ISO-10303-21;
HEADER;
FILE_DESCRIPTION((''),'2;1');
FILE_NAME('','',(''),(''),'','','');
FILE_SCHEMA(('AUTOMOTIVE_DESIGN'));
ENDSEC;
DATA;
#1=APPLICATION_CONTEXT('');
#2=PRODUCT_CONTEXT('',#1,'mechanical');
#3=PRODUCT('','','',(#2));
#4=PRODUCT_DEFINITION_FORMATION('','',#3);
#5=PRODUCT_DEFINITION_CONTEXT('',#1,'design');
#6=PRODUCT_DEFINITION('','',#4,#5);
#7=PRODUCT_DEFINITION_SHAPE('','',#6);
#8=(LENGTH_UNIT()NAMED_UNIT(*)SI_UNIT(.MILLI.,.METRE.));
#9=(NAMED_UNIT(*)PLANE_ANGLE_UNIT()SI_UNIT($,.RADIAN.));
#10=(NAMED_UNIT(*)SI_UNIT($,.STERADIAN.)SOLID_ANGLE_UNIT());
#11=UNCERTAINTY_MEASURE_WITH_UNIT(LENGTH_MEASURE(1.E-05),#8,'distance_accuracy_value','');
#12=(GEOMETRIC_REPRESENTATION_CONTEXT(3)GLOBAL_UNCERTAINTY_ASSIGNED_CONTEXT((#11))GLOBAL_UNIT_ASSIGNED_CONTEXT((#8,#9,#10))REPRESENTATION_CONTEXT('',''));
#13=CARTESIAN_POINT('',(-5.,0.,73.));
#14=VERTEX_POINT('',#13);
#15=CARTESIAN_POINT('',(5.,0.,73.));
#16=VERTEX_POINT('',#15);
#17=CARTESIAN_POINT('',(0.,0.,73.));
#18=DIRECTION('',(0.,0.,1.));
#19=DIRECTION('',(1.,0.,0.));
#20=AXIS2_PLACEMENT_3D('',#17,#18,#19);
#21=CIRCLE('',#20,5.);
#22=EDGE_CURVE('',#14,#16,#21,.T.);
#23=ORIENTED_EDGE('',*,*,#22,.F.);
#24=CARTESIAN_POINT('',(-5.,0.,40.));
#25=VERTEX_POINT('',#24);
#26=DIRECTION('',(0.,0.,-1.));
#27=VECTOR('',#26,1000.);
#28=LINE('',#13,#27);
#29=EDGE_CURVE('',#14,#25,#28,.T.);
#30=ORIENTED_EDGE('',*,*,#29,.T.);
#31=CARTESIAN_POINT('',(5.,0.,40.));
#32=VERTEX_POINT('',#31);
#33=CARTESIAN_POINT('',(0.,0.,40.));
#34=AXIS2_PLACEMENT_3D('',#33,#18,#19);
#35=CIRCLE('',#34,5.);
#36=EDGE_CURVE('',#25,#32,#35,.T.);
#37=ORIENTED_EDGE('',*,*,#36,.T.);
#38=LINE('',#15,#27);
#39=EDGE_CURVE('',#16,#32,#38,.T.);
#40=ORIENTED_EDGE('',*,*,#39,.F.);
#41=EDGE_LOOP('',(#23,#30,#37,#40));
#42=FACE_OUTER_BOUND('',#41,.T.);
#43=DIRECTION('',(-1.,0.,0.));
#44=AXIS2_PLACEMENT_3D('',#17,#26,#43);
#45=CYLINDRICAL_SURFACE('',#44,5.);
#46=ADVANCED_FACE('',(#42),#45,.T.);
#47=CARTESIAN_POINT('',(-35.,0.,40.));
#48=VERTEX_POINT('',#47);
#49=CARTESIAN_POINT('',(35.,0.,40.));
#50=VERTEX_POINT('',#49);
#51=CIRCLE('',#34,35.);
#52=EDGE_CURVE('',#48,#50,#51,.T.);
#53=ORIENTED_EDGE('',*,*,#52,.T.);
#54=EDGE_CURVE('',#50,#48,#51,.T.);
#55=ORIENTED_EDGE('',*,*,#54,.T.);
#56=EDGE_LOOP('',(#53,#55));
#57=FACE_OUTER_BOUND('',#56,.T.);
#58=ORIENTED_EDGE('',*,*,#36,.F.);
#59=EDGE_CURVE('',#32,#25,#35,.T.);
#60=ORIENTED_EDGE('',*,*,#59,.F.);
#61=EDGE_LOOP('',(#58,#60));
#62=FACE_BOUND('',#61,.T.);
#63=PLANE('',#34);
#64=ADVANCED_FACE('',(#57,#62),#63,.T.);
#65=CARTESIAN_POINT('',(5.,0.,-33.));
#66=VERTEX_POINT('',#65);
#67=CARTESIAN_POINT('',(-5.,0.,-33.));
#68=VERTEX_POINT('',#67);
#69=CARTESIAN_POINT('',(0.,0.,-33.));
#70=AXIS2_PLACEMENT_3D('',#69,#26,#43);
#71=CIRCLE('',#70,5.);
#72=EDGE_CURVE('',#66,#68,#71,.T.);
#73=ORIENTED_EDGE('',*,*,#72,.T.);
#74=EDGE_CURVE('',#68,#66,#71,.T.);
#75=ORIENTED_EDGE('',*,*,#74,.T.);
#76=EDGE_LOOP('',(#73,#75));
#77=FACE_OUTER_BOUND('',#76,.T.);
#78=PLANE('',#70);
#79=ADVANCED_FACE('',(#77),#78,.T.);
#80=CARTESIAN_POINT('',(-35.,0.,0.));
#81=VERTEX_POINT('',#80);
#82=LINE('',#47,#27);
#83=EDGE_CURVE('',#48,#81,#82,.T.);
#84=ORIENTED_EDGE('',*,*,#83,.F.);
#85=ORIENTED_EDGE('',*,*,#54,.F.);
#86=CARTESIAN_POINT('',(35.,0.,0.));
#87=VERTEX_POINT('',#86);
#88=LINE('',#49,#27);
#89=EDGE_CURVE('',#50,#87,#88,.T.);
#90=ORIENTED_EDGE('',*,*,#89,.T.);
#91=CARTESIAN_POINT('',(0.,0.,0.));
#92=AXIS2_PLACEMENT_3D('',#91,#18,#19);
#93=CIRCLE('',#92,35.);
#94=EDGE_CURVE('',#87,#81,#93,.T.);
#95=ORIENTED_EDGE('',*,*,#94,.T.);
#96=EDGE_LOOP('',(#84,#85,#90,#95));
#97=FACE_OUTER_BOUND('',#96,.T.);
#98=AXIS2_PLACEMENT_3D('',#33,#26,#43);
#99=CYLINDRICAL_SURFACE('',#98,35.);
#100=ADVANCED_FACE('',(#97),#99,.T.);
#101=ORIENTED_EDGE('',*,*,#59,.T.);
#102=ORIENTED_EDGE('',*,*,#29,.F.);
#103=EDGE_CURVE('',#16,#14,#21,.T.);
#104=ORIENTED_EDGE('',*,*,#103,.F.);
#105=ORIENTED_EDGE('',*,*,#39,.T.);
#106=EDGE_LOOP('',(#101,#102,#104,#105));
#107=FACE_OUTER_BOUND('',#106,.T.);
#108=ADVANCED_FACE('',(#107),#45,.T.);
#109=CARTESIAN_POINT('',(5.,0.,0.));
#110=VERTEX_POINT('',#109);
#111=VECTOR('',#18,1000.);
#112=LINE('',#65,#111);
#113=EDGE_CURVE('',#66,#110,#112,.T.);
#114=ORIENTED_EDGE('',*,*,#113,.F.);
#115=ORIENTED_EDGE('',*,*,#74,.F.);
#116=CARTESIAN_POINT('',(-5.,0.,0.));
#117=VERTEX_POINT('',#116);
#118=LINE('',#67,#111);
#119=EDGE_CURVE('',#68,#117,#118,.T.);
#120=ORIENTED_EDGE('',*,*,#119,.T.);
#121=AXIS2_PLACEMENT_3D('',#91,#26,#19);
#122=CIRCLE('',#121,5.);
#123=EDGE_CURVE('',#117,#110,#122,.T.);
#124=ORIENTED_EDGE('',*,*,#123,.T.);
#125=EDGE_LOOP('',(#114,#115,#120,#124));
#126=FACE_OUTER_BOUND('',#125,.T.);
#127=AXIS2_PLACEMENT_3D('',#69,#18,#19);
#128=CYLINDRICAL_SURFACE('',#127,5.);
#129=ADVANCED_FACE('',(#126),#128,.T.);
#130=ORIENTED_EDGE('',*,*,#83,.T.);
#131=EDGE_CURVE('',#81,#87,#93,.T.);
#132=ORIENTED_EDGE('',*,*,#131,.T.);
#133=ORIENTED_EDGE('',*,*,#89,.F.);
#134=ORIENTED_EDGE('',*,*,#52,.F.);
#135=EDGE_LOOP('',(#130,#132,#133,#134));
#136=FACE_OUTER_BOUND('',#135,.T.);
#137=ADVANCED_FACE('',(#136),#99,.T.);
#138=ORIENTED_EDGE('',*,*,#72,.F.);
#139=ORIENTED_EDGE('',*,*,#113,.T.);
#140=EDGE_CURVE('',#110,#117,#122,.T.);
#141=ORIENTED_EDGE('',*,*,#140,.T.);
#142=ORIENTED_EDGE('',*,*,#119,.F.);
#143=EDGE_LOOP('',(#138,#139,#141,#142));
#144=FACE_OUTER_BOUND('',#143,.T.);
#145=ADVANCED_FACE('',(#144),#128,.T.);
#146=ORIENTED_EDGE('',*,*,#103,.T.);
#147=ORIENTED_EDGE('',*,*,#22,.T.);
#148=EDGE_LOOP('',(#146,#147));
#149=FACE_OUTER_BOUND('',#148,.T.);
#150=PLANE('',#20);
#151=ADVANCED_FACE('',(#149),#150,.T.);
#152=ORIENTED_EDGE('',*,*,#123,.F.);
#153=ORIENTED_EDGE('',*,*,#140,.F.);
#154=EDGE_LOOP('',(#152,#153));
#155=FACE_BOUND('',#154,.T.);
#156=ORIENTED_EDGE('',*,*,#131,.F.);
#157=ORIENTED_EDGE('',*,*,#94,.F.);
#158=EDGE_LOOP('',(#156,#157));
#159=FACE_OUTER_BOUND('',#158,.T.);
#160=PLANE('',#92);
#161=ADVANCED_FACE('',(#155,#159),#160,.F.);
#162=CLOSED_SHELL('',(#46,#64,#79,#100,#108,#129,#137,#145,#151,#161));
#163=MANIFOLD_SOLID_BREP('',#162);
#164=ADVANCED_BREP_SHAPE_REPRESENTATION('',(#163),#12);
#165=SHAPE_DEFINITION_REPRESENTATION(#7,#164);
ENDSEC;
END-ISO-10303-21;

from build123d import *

# Parameters (mm, degrees)
SKETCH_1_R      = 35
EXTRUDE_1_DEPTH = 40
SKETCH_2_R      = 5
EXTRUDE_2_DEPTH = 33
EXTRUDE_START   = 33
SKETCH_3_R      = 5
EXTRUDE_3_DEPTH = 33


with BuildPart() as part:
    # 草图1 → 凸台-拉伸1 (new body)
    with BuildSketch(Plane.XY):
        Circle(SKETCH_1_R)
    extrude(amount=EXTRUDE_1_DEPTH)

    # 草图2 → 凸台-拉伸2 (add)
    with BuildSketch(Plane.XY.offset(40)):
        Circle(SKETCH_2_R)
    extrude(amount=EXTRUDE_2_DEPTH)

    # 草图3 → 凸台-拉伸3 (add)
    with BuildSketch(Plane(origin=(0, 0, 0), x_dir=(-1, 0, 0), z_dir=(0, 0, -1)).offset(EXTRUDE_START)):
        with Locations(Location((0, 0, 0), (0, 0, 180))):
            Circle(SKETCH_3_R)
    extrude(amount=-EXTRUDE_3_DEPTH)


solid = part.part
